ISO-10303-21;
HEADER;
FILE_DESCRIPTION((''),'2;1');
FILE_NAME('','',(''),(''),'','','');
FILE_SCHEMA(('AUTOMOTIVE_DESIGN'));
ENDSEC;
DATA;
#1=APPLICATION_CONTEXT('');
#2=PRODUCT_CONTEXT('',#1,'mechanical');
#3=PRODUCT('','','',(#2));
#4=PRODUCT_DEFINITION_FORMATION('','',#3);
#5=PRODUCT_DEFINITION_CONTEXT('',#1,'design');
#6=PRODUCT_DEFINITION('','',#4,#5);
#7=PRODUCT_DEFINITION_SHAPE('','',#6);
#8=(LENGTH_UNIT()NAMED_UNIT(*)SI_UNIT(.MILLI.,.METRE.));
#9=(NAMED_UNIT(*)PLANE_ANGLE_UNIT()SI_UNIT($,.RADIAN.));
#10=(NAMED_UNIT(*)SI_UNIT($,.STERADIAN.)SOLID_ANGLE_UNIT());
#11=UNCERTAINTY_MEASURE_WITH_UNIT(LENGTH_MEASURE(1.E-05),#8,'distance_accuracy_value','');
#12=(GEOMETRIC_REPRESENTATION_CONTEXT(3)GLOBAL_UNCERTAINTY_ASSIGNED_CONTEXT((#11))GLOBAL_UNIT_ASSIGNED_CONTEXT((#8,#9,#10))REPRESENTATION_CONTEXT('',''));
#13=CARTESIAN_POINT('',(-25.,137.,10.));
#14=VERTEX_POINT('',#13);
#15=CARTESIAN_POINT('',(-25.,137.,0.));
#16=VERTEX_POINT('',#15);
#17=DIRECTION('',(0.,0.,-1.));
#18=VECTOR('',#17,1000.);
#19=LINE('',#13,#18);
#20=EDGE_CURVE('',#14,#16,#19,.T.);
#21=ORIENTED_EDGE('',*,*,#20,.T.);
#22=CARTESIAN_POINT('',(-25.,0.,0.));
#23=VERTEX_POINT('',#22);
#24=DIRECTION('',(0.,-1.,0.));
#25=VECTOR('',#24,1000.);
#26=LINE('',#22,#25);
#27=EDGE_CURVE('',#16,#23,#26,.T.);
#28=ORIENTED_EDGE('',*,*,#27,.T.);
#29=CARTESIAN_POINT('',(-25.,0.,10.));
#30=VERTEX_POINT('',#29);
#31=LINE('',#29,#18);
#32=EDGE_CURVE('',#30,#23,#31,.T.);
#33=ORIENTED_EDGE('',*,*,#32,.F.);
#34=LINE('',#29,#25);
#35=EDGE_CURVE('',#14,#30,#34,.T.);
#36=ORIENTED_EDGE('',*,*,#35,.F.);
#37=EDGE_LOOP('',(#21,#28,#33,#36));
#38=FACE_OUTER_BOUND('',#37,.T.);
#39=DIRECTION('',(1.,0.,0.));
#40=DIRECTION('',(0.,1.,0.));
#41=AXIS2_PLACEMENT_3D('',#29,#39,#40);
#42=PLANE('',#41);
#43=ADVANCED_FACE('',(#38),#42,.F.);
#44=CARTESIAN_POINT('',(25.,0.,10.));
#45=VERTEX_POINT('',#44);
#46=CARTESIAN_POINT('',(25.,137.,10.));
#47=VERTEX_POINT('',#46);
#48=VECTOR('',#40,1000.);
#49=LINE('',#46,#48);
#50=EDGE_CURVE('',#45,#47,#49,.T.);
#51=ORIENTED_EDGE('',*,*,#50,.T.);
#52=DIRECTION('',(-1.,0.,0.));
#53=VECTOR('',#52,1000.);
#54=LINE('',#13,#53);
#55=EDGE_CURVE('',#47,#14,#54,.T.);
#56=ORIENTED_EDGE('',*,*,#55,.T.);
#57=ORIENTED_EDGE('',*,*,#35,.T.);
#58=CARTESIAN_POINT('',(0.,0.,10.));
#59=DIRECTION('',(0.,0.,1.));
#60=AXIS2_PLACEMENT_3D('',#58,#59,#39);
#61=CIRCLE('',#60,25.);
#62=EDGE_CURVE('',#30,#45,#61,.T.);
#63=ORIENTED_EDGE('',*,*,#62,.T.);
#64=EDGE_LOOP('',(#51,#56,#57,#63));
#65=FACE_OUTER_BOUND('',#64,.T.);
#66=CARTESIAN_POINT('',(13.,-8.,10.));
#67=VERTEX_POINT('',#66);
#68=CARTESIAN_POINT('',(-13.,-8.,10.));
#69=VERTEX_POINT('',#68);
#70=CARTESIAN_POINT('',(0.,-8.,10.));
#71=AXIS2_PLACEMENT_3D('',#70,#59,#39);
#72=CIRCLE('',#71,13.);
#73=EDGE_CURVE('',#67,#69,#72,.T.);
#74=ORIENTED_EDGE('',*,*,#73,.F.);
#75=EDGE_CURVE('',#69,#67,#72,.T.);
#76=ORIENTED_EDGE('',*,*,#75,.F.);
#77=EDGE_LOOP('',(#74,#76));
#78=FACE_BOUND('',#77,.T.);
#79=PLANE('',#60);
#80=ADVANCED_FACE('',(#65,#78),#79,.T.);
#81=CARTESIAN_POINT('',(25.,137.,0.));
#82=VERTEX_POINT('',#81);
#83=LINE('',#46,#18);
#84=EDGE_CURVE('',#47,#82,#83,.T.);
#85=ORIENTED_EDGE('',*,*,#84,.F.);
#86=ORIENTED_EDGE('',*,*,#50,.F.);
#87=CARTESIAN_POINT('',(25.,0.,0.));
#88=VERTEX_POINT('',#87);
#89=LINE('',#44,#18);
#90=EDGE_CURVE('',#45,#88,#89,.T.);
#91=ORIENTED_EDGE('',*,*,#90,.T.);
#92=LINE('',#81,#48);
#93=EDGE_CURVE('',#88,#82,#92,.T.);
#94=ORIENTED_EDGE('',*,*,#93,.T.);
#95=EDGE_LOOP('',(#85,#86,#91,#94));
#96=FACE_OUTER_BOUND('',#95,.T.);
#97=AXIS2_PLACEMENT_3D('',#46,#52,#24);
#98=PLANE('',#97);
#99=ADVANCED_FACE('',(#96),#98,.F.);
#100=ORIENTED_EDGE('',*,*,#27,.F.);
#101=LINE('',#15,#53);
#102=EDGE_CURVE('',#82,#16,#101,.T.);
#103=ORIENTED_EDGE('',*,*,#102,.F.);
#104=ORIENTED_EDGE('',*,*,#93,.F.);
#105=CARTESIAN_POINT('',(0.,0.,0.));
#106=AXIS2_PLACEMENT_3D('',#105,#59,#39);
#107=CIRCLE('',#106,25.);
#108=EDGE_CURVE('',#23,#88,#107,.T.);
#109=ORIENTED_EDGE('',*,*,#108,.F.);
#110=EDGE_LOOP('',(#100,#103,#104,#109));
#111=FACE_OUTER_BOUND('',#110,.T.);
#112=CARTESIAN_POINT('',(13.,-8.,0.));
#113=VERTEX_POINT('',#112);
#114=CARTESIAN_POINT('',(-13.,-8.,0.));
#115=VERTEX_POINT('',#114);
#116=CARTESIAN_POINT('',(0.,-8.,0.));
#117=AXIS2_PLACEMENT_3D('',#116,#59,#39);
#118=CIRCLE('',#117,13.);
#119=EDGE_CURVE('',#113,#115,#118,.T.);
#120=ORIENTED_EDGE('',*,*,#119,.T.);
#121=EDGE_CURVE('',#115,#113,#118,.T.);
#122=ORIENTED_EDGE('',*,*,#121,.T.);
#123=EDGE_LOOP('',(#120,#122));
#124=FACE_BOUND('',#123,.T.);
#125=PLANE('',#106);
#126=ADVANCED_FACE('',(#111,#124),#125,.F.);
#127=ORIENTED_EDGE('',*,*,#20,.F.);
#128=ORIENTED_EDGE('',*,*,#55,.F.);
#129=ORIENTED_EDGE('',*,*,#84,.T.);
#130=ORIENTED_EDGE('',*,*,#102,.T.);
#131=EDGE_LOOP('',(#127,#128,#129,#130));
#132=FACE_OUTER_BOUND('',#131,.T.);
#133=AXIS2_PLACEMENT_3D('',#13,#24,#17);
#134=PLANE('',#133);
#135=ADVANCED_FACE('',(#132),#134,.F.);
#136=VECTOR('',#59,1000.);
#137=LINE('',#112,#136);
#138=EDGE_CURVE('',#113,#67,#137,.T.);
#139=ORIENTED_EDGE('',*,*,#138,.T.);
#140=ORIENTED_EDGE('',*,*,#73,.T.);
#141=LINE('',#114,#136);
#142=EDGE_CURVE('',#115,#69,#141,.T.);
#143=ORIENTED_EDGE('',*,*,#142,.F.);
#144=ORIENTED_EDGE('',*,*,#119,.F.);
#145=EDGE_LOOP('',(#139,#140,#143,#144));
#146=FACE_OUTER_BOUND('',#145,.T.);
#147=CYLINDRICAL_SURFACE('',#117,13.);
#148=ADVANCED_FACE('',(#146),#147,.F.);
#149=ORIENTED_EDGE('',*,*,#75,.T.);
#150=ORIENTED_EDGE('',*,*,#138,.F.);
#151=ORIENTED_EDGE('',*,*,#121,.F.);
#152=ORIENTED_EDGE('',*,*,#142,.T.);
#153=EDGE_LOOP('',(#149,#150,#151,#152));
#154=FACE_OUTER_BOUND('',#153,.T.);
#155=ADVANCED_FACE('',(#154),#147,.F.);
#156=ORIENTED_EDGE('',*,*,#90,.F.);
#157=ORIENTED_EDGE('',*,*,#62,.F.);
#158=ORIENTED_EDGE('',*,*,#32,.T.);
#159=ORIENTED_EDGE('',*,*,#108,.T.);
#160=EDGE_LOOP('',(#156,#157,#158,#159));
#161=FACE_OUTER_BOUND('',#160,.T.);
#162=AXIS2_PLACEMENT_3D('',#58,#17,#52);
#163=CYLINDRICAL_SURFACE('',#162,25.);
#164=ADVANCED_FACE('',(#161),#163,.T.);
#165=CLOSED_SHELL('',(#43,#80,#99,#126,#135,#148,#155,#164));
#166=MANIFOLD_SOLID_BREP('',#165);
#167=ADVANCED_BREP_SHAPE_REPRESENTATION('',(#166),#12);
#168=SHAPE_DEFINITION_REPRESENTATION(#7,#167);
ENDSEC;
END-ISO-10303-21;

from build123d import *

# Parameters (mm, degrees)
BOSS_EXTRUDE1_DEPTH = 10
SKETCH2_R           = 13
CUT_EXTRUDE1_DEPTH  = 140.620915339


with BuildPart() as part:
    # Sketch1 → Boss-Extrude1 (new body)
    with BuildSketch(Plane.XY):
        with BuildLine():
            Line((-25, 0), (-25, 137))
            Line((-25, 137), (25, 137))
            Line((25, 137), (25, 0))
            ThreePointArc((25, 0), (0, -25), (-25, 0))
        make_face()
    extrude(amount=BOSS_EXTRUDE1_DEPTH)

    # Sketch2 → Cut-Extrude1 (cut, through all)
    with BuildSketch(Plane.XY.offset(10)):
        with Locations((0, -8)):
            Circle(SKETCH2_R)
    extrude(amount=-CUT_EXTRUDE1_DEPTH, mode=Mode.SUBTRACT)


solid = part.part
